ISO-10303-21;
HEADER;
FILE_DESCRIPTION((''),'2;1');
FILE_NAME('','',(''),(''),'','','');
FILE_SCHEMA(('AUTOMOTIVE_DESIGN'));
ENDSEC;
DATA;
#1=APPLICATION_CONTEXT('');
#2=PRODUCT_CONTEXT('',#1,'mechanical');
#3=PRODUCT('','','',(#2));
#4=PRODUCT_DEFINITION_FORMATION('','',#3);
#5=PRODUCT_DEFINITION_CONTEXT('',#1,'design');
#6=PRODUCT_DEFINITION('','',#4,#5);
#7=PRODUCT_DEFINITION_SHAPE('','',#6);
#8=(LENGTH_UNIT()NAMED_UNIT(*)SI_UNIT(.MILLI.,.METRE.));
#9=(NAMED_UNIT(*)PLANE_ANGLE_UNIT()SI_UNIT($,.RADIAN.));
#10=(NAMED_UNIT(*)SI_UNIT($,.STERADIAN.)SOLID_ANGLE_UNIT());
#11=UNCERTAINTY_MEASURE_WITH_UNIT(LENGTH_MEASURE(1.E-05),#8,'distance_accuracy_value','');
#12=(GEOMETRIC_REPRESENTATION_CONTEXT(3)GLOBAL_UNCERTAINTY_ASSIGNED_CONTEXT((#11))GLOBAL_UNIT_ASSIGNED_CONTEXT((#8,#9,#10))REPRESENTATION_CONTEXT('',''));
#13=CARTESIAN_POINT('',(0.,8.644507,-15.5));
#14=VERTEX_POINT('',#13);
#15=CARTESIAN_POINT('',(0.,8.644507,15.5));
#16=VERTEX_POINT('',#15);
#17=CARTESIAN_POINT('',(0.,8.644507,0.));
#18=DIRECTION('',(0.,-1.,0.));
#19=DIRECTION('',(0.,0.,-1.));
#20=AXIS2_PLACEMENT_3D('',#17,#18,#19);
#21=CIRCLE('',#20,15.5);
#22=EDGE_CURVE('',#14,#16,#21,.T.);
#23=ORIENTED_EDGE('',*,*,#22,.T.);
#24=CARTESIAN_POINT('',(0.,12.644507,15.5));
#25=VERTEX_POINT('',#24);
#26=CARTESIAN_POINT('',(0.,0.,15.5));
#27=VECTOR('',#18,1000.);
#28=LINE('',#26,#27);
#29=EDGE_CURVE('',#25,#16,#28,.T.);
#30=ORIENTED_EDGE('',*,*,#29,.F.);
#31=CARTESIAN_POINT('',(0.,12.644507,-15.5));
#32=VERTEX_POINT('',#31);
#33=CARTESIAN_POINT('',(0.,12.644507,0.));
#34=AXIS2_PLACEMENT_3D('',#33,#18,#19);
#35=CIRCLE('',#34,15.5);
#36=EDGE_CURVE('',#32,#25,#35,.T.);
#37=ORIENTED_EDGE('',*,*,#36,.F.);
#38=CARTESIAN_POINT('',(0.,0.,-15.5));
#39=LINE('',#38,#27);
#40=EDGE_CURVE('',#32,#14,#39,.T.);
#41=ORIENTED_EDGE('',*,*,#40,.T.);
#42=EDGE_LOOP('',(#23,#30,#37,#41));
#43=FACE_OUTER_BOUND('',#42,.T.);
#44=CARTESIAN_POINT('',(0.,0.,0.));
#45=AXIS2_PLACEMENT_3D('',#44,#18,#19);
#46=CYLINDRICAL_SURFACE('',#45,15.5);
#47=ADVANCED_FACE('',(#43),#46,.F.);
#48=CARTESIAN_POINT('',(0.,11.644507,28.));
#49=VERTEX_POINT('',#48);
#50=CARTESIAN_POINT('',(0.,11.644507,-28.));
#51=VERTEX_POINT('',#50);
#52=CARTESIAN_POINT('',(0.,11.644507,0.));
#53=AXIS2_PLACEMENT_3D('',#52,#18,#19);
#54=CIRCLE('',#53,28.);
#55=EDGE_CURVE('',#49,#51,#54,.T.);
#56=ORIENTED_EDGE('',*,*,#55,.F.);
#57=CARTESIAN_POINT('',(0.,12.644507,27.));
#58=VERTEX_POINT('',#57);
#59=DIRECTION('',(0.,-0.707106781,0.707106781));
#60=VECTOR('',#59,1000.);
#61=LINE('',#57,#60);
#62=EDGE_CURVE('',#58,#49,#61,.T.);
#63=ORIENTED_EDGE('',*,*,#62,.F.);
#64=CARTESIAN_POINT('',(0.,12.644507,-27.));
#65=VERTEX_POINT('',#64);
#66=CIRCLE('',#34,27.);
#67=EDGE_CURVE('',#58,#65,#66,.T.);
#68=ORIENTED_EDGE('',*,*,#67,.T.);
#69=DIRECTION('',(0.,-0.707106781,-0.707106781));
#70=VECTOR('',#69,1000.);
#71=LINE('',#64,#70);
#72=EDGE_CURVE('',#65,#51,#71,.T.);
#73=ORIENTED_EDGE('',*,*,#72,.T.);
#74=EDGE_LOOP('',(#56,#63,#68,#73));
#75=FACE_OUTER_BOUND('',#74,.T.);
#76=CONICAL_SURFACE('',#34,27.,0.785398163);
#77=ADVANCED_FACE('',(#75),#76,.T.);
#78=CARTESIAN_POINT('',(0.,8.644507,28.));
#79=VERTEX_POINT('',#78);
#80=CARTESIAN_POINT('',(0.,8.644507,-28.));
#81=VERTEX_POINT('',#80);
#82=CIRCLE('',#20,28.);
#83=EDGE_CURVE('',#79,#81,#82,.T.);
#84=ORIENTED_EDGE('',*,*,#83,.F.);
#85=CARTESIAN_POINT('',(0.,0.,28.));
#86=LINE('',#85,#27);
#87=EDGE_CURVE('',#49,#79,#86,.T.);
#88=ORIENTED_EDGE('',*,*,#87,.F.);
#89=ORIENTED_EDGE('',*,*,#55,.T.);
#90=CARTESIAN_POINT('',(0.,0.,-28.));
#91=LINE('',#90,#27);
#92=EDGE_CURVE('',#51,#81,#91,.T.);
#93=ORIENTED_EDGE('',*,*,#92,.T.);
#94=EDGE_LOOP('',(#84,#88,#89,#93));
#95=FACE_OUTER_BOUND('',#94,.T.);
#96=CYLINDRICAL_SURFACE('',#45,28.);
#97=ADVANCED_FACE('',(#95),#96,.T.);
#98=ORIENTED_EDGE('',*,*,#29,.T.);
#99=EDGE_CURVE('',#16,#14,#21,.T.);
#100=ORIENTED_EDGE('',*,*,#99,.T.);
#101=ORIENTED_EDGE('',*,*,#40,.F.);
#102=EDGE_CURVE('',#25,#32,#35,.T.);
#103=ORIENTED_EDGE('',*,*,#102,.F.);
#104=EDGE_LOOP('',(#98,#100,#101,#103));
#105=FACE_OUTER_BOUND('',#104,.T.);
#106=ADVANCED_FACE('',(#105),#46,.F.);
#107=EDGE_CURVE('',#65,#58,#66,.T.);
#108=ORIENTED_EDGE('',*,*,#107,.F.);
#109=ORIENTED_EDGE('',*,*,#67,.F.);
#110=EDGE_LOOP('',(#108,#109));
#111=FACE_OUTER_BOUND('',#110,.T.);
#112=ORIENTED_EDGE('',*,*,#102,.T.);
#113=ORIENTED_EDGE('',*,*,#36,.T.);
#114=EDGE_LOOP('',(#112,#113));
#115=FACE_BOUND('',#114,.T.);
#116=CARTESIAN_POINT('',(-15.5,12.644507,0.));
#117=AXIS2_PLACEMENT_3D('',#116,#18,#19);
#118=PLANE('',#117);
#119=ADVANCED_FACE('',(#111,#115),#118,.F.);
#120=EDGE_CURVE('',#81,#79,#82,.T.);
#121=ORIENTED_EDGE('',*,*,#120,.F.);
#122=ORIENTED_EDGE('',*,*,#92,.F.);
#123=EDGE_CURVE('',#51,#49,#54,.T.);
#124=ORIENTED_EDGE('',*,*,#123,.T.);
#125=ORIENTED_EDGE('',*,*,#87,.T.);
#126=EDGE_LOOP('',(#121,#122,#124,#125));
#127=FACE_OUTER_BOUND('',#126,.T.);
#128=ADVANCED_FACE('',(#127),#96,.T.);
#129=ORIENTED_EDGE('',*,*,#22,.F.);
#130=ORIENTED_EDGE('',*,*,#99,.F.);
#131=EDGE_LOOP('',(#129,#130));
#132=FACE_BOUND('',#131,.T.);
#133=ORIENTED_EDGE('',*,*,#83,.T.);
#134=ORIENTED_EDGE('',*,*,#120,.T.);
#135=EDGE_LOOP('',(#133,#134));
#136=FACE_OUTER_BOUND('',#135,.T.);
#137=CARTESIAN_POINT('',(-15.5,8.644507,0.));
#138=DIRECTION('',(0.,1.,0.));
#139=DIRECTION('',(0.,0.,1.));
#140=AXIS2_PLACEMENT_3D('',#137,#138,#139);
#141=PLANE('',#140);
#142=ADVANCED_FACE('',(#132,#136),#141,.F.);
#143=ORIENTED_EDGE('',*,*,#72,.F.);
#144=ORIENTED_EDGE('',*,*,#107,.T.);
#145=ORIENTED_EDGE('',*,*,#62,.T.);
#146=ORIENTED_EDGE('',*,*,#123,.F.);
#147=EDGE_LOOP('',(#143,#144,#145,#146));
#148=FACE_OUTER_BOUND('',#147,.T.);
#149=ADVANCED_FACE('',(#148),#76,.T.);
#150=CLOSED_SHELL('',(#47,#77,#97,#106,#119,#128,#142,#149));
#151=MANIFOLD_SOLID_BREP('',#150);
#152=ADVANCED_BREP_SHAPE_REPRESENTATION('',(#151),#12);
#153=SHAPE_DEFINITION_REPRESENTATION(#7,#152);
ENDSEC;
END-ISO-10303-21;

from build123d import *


with BuildPart() as part:
    # 草图1 → Revolve 432 (revolve)
    with BuildSketch(Plane.XY, mode=Mode.PRIVATE) as revolve_432_sk:
        Polygon((-27, 12.644507042), (-28, 11.644507042), (-28, 8.644507042), (-15.5, 8.644507042), (-15.5, 12.644507042), align=None)
    revolve(revolve_432_sk.sketch.rotate(Axis((0, 0, 0), (0, 1, 0)), 270), axis=Axis((0, 0, 0), (0, 1, 0)))


solid = part.part
